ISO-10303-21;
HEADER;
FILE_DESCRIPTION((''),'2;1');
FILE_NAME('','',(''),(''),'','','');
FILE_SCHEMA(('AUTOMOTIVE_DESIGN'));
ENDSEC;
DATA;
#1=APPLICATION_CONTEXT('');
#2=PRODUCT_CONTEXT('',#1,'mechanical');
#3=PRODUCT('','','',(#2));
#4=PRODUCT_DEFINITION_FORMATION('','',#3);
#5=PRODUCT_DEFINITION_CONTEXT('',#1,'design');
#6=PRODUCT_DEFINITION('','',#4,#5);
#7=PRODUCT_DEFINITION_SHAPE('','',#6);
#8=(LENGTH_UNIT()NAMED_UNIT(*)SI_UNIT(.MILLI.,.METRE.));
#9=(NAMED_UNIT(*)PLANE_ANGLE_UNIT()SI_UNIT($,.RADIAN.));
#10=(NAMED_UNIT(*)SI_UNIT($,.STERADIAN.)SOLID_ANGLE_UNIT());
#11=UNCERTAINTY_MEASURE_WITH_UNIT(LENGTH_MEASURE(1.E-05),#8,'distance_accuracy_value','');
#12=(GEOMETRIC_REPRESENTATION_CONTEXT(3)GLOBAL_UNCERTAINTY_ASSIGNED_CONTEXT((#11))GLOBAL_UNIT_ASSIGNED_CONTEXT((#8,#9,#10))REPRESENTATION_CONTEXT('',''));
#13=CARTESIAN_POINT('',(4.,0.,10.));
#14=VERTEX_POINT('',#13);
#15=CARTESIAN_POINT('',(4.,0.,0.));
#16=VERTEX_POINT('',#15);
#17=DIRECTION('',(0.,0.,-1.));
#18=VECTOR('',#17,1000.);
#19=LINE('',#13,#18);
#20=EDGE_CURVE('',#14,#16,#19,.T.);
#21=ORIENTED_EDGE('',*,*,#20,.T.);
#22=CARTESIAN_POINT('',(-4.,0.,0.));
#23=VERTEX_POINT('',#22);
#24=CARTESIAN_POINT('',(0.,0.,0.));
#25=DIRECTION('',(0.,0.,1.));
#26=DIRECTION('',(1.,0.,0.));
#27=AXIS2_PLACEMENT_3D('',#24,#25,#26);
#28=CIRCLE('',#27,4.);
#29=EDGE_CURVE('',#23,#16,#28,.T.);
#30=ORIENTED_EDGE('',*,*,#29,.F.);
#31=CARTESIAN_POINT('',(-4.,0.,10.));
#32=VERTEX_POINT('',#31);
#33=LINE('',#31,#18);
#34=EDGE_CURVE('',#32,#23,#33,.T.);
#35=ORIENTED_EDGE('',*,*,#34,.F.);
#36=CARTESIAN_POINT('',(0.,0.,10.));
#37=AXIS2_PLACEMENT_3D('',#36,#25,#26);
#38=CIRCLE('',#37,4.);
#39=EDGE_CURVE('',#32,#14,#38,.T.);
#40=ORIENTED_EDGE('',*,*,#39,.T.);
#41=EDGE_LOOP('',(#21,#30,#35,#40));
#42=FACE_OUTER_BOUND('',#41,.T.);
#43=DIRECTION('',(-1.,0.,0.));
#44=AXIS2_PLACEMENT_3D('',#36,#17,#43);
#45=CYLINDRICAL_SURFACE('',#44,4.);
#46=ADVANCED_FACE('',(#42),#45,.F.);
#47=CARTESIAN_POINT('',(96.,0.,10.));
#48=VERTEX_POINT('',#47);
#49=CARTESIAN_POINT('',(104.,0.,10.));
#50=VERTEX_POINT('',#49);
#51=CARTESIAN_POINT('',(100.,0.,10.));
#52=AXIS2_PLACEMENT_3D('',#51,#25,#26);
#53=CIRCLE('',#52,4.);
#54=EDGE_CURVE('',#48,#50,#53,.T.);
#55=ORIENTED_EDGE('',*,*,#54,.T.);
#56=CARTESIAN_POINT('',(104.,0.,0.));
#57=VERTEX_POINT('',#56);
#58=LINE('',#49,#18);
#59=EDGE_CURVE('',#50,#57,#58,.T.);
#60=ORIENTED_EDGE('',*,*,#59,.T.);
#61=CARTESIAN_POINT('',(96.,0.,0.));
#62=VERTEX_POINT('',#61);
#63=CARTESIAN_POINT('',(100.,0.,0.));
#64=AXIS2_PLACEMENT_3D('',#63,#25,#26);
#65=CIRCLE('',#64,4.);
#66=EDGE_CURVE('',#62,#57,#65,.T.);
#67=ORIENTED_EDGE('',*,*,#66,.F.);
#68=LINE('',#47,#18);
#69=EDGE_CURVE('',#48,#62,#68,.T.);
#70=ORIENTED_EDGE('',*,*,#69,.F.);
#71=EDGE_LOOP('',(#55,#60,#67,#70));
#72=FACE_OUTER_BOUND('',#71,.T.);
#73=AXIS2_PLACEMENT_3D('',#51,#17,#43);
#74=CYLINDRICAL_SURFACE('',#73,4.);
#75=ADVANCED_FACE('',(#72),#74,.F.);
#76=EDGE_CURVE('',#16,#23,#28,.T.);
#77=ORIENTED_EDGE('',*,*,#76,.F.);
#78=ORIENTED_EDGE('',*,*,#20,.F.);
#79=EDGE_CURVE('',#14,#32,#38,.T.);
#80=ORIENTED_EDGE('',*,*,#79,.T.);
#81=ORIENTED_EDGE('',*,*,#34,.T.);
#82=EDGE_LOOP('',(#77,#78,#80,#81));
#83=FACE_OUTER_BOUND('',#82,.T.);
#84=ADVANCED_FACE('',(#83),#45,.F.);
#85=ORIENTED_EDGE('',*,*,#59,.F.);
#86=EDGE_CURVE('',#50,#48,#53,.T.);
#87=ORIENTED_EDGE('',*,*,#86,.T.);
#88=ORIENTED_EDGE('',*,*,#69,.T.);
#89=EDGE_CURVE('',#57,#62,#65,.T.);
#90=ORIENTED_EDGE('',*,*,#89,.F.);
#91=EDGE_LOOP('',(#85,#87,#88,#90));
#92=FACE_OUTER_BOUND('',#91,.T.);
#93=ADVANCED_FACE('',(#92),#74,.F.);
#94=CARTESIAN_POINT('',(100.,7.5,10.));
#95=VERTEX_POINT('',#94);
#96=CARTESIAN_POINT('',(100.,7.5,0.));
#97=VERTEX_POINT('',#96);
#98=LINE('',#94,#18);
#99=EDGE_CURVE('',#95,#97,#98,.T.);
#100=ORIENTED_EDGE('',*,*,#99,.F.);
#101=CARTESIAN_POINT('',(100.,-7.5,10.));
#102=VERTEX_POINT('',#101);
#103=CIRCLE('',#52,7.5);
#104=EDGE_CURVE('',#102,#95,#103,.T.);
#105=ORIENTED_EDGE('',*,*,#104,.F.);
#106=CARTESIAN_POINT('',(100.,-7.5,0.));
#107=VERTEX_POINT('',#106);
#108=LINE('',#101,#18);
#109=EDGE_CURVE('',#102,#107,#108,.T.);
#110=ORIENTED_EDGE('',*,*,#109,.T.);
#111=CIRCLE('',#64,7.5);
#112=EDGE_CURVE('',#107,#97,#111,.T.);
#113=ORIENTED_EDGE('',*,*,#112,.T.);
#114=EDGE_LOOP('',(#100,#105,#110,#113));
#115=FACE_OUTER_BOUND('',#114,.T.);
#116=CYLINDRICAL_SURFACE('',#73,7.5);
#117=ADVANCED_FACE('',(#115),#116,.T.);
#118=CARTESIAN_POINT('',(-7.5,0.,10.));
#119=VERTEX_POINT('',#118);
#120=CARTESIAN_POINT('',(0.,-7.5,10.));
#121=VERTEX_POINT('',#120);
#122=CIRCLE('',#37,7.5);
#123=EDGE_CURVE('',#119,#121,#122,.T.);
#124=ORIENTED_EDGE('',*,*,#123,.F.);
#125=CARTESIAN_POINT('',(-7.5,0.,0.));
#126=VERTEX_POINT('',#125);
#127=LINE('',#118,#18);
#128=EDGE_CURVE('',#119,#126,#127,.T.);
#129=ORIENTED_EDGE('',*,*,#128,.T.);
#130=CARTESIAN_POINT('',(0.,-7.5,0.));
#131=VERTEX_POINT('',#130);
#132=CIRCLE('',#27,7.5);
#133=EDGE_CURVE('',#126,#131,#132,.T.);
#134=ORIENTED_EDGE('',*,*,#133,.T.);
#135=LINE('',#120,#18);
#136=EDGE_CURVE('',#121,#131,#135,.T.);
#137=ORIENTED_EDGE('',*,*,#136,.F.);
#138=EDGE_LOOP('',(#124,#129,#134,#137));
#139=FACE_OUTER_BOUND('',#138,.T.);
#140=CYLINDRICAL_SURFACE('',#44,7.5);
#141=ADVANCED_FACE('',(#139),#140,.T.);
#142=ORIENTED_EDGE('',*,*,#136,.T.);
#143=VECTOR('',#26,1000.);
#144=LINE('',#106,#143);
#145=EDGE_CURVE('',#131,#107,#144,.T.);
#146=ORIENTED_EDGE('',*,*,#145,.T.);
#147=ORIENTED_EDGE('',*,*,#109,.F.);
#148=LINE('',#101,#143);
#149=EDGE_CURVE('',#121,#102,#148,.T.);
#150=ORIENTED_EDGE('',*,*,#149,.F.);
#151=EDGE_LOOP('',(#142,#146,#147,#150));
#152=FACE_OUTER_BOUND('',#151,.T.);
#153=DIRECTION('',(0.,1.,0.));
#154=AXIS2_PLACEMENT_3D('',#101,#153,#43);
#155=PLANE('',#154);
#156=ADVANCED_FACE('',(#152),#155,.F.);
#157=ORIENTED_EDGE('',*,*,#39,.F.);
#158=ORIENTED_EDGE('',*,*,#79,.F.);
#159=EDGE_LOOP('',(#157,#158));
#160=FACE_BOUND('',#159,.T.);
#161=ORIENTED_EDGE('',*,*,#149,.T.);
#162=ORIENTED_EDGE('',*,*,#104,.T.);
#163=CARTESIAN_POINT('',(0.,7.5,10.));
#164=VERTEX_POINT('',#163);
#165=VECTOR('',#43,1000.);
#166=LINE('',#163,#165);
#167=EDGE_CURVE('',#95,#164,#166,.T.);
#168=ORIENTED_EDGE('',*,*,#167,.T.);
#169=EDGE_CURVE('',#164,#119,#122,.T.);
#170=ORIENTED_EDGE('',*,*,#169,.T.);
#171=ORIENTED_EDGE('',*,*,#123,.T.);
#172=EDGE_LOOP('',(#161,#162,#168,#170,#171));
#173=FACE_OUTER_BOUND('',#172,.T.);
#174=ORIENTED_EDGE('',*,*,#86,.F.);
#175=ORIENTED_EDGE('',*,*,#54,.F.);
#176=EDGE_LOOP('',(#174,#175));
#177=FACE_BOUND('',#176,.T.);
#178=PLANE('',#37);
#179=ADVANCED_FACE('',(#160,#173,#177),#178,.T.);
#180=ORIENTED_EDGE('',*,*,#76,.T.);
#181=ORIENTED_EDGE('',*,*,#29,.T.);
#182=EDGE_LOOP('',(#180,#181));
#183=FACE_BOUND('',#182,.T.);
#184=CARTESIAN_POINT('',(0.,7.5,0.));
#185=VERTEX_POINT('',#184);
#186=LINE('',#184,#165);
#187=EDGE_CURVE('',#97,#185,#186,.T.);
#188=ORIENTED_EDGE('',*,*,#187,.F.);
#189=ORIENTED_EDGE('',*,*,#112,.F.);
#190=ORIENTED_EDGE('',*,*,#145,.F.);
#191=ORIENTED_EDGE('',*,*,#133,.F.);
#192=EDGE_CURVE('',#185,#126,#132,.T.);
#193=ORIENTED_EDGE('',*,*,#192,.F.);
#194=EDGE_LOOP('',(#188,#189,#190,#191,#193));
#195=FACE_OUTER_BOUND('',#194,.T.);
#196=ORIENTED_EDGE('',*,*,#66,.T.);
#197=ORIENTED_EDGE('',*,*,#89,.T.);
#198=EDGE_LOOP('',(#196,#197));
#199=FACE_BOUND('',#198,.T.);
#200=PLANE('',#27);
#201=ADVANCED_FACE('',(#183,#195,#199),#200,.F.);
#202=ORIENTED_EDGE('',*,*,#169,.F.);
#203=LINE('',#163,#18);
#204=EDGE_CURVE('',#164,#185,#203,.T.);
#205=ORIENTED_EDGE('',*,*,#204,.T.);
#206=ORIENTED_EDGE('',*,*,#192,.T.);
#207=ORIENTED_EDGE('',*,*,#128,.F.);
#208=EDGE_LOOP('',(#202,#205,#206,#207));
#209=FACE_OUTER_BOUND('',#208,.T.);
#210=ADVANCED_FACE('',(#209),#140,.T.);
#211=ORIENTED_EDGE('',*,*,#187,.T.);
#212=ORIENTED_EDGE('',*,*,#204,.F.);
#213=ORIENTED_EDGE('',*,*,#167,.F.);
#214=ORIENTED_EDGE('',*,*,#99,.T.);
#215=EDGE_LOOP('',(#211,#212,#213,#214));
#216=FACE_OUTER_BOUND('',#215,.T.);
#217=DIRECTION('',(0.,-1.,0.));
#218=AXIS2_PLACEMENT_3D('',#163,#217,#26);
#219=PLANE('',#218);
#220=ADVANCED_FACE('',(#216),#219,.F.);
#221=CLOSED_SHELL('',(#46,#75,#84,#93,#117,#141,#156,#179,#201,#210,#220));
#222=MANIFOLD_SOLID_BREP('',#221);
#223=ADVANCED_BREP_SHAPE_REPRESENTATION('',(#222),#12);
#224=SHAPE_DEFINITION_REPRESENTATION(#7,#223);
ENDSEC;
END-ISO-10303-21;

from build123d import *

# Parameters (mm, degrees)
SKETCH1_R           = 4
BOSS_EXTRUDE1_DEPTH = 10


with BuildPart() as part:
    # Sketch1 → Boss-Extrude1 (new body)
    with BuildSketch(Plane.XY):
        with BuildLine():
            Line((0, 7.5), (100, 7.5))
            ThreePointArc((100, 7.5), (107.5, 0), (100, -7.5))
            Line((100, -7.5), (0, -7.5))
            ThreePointArc((0, -7.5), (-7.5, 0), (0, 7.5))
        make_face()
        Circle(SKETCH1_R, mode=Mode.SUBTRACT)
        with Locations((100, 0)):
            Circle(SKETCH1_R, mode=Mode.SUBTRACT)
    extrude(amount=BOSS_EXTRUDE1_DEPTH)


solid = part.part
